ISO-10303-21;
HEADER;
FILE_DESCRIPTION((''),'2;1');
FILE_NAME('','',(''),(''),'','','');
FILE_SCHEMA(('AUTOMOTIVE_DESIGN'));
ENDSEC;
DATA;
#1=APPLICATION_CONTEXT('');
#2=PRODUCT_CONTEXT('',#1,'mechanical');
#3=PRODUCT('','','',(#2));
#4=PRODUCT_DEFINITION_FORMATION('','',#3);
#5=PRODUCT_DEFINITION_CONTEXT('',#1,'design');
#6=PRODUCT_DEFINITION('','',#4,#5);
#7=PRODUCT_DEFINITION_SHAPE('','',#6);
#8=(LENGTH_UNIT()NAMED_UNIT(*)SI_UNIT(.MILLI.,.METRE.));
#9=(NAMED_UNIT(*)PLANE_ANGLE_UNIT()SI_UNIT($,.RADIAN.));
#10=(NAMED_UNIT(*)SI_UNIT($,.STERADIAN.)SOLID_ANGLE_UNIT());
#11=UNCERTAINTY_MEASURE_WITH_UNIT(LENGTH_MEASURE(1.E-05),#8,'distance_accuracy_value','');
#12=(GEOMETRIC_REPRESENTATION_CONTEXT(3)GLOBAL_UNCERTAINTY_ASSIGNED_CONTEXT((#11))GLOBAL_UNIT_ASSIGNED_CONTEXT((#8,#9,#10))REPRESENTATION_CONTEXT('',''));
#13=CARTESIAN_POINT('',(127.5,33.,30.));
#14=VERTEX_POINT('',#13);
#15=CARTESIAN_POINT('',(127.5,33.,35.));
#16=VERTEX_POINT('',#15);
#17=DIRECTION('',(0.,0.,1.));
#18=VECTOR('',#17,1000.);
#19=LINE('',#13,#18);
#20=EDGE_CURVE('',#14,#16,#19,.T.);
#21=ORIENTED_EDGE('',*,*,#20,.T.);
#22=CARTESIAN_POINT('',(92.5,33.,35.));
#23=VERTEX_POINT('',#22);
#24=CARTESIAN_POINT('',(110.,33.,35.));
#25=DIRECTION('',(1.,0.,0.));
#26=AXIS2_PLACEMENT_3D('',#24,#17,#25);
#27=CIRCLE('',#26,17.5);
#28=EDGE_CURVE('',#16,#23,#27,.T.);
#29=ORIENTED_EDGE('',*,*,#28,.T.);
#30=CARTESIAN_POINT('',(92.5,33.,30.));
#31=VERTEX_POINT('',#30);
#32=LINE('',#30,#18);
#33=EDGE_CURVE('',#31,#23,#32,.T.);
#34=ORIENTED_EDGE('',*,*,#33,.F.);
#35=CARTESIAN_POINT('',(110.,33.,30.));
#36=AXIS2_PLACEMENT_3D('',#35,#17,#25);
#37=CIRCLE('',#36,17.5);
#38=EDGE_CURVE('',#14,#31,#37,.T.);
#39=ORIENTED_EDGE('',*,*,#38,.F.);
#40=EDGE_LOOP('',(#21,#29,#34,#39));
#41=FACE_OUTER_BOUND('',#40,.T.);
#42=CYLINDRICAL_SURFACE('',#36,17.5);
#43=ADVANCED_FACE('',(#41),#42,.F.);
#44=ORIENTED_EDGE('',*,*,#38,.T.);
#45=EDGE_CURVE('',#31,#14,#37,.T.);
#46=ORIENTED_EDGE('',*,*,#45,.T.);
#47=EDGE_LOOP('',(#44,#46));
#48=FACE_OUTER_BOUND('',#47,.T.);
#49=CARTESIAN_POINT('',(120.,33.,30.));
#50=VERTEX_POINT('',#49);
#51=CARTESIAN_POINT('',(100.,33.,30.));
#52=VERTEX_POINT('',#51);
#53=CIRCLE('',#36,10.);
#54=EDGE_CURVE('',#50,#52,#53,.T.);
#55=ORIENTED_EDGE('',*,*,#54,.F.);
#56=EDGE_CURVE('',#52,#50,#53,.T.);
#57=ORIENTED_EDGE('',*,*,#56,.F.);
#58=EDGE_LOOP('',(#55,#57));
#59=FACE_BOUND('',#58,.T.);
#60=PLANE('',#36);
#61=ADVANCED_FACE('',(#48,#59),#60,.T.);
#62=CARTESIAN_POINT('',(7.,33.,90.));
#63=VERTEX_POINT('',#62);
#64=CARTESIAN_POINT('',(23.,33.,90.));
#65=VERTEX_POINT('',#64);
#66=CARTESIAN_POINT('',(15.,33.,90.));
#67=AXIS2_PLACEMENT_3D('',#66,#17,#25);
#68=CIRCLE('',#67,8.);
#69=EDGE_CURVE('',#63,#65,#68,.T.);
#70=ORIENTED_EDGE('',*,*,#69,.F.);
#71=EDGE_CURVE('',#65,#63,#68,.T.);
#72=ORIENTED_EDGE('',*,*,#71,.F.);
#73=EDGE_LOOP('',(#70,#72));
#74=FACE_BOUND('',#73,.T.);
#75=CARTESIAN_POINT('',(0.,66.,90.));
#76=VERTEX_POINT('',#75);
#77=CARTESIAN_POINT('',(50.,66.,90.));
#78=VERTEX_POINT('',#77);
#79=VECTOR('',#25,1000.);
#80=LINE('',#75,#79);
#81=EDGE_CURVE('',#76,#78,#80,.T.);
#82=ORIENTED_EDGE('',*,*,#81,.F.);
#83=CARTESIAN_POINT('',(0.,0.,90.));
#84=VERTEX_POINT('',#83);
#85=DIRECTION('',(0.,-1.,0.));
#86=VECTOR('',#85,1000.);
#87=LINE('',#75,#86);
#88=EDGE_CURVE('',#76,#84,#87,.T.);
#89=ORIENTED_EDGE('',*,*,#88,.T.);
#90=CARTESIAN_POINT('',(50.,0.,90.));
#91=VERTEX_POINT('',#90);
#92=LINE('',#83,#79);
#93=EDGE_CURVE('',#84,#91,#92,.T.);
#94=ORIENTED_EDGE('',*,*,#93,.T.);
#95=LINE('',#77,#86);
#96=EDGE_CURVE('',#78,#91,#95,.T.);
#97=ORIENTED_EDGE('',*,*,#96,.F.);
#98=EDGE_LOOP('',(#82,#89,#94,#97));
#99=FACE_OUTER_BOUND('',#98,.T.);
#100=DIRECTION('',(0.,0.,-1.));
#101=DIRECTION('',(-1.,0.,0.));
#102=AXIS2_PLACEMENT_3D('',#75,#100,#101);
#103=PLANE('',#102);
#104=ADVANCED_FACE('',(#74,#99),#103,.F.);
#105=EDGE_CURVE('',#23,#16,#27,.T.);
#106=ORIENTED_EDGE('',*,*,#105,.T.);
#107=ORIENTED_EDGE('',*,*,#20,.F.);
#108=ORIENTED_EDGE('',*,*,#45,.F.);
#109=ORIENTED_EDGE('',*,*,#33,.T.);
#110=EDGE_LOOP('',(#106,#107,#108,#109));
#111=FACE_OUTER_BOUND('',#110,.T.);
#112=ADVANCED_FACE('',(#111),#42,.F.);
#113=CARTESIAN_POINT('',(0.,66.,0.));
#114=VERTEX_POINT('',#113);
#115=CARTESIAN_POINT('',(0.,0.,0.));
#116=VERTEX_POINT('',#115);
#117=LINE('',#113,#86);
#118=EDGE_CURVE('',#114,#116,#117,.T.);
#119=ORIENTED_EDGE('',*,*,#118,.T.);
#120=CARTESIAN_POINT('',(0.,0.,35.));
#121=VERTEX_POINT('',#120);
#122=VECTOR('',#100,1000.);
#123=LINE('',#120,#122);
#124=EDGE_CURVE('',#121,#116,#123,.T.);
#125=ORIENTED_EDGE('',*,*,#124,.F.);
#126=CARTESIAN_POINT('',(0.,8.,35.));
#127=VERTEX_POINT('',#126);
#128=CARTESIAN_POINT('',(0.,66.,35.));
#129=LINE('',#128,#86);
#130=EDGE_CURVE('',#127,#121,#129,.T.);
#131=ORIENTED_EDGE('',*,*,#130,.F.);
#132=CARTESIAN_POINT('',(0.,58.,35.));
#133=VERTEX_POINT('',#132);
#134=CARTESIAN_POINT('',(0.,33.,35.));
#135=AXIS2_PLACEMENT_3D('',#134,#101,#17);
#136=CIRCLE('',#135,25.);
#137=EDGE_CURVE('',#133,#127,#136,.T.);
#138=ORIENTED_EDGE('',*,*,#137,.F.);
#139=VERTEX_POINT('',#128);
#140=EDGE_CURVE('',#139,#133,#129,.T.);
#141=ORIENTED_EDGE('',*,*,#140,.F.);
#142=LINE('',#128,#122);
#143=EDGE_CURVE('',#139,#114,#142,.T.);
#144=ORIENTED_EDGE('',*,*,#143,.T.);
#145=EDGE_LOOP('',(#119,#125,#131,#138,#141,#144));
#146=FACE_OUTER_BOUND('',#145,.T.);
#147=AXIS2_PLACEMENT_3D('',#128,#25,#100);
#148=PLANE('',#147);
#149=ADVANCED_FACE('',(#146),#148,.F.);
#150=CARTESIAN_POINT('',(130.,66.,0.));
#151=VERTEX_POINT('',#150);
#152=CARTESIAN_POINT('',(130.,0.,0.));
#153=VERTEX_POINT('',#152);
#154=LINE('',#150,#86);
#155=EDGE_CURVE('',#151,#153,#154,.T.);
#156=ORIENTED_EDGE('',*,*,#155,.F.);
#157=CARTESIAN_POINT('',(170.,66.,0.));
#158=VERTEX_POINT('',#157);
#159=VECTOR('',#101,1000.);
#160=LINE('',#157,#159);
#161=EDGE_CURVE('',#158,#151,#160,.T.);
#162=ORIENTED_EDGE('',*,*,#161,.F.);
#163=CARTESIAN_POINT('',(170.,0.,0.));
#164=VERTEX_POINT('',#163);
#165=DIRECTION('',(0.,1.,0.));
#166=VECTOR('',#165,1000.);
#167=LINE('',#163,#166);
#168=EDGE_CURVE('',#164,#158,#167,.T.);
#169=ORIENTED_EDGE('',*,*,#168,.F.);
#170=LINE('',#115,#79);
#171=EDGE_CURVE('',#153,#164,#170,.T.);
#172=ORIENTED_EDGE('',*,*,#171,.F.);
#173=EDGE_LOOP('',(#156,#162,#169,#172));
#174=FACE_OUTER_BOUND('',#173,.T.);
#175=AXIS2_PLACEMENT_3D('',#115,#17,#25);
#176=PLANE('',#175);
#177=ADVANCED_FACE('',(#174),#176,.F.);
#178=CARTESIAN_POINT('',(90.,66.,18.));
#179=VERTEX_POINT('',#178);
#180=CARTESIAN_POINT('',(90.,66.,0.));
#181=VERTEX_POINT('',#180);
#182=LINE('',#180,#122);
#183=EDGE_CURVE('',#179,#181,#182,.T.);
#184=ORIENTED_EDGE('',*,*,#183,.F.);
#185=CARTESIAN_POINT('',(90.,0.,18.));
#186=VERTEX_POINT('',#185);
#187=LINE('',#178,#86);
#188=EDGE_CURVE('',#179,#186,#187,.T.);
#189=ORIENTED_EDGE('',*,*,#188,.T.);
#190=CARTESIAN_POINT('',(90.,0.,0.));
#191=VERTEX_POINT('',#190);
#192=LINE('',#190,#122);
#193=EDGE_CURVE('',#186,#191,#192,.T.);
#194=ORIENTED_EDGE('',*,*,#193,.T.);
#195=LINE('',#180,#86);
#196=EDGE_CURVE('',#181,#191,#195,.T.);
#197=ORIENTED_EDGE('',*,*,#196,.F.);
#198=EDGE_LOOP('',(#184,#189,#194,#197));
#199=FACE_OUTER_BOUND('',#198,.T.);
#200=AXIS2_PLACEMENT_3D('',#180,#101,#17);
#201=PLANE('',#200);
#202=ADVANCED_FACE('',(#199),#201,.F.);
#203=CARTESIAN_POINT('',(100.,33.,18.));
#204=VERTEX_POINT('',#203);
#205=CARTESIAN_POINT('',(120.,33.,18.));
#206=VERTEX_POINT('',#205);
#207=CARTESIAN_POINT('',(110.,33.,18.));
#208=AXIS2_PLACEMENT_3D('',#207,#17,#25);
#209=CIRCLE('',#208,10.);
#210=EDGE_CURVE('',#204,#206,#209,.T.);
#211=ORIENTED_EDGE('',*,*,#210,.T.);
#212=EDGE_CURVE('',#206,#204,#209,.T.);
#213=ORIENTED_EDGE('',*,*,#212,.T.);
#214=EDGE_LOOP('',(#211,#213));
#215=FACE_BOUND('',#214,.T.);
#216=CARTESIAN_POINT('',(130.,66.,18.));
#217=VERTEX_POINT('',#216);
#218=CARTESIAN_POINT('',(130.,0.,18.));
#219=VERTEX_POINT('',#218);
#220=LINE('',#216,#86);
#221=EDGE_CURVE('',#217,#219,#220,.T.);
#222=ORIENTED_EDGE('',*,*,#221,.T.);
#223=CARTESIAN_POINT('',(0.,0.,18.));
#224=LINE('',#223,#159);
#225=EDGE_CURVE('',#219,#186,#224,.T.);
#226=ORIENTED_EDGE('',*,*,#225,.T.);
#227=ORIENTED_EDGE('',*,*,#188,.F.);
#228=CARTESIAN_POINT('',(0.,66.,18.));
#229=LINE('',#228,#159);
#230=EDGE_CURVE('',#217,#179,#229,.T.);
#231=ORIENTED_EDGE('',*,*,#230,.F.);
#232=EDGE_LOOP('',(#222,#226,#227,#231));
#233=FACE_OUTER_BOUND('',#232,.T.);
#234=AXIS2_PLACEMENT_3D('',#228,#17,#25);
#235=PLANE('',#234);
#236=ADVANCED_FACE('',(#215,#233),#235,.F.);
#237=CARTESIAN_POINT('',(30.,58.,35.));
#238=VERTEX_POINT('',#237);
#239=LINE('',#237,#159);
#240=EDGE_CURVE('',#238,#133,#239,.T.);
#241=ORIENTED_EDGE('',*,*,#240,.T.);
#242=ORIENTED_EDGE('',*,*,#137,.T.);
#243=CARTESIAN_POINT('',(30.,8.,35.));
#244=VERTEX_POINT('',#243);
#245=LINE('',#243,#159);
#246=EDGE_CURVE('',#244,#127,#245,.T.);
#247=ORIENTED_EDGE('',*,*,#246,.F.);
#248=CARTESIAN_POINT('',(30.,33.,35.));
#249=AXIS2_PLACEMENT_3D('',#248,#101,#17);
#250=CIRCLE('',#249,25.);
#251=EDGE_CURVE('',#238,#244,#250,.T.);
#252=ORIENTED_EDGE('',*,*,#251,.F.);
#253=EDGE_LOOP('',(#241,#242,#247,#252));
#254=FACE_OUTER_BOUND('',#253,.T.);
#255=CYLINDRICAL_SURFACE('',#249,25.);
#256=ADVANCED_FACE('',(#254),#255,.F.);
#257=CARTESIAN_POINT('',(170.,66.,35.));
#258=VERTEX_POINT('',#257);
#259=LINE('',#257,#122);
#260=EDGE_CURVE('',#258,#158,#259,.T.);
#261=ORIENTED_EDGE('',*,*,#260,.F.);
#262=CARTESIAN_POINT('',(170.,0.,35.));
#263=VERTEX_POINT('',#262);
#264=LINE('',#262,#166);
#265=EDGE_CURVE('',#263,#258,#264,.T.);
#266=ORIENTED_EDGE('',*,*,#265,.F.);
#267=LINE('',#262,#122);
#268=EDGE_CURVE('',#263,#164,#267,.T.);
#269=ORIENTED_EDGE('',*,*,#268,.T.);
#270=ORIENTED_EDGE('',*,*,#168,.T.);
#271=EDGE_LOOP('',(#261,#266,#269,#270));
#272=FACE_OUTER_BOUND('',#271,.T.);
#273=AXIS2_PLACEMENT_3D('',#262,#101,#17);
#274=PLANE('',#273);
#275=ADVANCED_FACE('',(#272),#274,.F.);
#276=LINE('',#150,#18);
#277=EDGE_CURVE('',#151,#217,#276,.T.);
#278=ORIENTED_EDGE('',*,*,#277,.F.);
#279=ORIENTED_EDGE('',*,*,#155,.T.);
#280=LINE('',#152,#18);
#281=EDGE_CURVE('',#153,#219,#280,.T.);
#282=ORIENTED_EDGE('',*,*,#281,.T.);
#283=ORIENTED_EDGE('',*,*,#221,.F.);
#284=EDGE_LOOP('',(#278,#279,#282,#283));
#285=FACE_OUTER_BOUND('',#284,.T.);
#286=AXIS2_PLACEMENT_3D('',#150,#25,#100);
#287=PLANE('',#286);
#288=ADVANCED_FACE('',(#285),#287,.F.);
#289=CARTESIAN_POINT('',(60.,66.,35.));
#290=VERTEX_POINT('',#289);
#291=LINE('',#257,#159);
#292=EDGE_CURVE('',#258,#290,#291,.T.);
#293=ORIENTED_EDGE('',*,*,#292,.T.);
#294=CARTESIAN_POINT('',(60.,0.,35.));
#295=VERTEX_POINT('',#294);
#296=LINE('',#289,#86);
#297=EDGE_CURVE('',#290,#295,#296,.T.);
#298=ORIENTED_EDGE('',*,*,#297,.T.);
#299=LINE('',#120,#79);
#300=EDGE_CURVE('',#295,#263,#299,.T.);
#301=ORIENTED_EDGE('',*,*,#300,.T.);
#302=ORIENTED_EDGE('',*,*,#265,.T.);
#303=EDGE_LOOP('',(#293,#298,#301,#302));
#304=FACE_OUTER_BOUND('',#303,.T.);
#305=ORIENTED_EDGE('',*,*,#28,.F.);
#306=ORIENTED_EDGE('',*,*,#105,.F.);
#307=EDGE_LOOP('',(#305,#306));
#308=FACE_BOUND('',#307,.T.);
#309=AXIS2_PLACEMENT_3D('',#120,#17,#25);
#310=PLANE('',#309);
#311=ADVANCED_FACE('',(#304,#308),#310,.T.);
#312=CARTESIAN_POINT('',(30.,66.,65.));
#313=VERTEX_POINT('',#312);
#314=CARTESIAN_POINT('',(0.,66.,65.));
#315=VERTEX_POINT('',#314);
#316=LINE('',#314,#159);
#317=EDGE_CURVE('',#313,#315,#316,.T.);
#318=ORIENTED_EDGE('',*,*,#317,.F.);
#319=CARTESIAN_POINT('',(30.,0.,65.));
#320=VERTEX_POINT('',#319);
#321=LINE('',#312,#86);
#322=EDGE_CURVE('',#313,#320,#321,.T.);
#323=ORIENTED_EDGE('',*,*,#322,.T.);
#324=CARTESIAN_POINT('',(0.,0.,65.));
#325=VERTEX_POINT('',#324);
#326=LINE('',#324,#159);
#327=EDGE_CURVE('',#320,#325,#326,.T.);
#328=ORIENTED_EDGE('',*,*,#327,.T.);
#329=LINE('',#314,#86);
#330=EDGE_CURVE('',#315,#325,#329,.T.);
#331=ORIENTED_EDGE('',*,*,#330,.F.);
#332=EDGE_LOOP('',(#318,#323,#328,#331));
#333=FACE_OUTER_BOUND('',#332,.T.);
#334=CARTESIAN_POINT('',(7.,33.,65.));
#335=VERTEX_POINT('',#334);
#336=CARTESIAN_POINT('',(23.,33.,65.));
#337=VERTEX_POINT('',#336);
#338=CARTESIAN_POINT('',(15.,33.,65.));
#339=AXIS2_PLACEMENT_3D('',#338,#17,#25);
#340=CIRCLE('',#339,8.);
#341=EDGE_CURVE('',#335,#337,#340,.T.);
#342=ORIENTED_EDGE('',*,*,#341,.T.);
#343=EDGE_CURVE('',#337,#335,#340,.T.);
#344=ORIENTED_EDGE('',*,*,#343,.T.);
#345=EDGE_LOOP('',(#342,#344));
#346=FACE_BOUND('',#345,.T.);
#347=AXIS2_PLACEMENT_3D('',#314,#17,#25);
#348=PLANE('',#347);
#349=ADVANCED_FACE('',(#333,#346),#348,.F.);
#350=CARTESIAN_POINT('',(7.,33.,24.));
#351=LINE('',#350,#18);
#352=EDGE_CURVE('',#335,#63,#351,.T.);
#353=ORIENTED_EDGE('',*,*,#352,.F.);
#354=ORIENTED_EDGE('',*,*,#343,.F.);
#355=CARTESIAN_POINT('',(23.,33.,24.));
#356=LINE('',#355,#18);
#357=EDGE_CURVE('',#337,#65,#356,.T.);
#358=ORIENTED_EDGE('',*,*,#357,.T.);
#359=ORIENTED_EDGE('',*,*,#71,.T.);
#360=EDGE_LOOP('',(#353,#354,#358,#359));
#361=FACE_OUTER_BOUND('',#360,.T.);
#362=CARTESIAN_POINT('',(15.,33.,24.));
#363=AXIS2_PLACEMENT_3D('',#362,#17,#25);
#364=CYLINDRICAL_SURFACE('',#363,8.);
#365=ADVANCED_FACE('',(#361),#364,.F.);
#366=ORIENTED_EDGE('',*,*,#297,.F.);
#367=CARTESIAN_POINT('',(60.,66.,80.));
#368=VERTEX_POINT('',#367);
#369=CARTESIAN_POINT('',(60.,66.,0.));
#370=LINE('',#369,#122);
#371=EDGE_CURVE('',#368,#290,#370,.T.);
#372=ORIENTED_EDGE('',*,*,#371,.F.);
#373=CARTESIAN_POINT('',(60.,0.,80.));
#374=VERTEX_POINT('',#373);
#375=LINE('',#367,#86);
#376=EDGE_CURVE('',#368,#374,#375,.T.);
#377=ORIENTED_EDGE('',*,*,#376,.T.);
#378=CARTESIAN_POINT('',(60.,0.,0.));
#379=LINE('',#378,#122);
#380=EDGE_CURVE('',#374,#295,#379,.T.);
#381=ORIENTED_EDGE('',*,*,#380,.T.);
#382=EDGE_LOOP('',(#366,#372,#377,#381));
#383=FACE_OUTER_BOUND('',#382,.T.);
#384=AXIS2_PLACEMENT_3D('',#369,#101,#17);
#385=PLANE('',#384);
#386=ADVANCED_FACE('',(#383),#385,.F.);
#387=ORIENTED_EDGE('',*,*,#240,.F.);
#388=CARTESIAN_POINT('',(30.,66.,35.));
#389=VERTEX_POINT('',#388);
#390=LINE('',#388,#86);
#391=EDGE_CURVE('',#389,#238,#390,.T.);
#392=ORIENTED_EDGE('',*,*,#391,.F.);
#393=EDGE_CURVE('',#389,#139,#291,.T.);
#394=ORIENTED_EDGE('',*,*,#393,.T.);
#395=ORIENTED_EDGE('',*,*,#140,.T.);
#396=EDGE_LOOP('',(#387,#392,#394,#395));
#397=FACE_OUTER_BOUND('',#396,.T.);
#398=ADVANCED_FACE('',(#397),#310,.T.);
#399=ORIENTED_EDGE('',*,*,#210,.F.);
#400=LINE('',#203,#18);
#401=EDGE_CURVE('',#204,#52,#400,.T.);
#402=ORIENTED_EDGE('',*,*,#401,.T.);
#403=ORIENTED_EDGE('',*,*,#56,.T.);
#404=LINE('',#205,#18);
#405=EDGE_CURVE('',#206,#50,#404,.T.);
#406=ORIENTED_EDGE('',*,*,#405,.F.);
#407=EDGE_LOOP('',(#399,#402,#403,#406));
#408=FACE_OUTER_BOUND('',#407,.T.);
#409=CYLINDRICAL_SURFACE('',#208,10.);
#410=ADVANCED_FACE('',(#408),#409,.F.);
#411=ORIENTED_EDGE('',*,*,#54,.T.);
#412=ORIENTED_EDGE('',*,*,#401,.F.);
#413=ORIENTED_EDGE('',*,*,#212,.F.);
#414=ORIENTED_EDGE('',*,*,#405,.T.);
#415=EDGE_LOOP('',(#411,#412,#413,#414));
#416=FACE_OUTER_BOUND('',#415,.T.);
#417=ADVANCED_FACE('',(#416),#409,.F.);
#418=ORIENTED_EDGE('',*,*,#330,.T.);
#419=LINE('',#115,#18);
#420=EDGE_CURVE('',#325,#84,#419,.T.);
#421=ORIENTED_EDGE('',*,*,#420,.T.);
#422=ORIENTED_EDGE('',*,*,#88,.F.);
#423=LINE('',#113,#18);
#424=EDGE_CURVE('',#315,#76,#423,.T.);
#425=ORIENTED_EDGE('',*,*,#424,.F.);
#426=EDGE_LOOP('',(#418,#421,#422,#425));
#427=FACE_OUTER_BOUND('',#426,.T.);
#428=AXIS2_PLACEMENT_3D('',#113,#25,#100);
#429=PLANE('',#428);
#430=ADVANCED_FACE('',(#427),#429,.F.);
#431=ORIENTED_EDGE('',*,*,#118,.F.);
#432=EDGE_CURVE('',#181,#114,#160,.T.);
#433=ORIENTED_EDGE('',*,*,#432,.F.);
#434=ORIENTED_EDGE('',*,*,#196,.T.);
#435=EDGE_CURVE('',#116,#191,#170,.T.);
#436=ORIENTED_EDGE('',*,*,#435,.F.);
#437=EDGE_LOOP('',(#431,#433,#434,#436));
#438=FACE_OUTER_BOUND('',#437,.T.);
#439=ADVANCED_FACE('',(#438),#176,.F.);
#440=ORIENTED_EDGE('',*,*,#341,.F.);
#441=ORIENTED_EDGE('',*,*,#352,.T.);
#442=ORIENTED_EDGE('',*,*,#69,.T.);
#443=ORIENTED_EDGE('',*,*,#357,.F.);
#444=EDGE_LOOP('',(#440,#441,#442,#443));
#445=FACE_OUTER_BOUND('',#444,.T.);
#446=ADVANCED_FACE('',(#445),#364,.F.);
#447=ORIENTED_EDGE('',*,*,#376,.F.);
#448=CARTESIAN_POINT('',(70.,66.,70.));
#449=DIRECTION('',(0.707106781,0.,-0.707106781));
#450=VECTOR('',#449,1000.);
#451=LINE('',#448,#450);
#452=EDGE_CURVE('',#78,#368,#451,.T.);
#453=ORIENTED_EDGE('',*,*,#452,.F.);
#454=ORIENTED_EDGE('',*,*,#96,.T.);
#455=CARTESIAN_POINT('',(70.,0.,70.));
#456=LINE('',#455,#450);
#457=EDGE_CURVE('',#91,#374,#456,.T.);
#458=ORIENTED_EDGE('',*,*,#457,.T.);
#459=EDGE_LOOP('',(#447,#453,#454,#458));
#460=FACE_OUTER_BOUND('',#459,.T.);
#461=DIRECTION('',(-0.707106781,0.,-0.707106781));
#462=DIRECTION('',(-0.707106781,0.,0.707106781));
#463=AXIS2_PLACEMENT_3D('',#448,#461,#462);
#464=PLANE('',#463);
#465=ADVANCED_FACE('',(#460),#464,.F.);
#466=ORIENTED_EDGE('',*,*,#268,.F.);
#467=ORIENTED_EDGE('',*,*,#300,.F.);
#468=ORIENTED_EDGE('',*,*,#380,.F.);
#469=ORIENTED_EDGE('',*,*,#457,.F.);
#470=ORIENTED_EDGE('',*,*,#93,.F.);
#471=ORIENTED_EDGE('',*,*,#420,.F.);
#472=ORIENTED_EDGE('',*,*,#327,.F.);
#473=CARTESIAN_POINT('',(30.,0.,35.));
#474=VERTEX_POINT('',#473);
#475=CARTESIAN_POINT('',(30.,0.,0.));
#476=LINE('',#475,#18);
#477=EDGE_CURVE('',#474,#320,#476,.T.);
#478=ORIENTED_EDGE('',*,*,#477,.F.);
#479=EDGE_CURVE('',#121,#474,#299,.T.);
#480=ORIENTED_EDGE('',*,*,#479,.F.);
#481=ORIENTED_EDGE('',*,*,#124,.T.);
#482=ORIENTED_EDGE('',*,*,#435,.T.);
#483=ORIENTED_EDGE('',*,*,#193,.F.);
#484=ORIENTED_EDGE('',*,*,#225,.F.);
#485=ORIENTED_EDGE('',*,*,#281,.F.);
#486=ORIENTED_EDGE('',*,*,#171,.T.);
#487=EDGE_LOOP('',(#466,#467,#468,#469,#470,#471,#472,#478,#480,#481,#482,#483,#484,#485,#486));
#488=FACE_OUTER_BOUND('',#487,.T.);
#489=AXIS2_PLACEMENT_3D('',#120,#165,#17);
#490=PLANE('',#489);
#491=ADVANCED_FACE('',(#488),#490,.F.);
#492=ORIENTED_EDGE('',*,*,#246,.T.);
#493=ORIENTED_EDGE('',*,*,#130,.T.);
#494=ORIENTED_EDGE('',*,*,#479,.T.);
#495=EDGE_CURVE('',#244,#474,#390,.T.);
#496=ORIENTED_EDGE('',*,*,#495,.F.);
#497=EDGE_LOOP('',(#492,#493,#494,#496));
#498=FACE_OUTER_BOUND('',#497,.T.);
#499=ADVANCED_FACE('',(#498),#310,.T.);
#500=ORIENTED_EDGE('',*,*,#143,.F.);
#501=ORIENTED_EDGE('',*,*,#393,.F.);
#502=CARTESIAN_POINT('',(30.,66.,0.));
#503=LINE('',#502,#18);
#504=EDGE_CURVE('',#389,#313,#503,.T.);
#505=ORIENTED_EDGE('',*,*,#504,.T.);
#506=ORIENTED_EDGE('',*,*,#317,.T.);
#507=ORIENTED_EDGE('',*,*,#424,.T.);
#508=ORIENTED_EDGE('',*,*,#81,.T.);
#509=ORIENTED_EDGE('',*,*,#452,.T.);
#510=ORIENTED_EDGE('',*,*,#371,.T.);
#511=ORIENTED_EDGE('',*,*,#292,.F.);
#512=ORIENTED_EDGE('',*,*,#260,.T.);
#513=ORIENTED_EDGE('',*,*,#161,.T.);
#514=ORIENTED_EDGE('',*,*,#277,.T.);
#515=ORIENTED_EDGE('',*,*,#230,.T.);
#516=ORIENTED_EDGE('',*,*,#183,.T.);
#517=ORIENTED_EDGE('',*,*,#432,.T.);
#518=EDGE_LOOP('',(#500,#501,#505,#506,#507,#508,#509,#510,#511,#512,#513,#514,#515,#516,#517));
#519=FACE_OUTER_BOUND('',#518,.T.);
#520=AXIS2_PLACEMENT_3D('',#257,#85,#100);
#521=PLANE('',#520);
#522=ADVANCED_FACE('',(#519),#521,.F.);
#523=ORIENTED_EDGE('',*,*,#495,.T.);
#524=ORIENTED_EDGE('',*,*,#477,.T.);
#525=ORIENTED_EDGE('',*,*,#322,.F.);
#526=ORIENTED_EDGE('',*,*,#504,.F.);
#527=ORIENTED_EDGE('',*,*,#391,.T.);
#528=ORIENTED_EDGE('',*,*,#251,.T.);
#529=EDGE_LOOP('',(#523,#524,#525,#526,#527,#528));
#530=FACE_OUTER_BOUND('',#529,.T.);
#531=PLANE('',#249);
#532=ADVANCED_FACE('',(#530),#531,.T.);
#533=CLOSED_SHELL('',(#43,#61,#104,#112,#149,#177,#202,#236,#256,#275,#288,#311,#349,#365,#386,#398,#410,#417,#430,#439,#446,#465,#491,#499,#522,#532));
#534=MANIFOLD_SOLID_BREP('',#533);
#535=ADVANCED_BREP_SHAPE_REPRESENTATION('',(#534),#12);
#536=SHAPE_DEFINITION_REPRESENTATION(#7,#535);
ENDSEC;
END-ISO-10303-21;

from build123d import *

# Parameters (mm, degrees)
BASE_BLOCK_PROFILE_W    = 170
BASE_BLOCK_PROFILE_H    = 66
BASE_BLOCK_DEPTH        = 35
SLOT_CUT_DEPTH          = 66
COUNTERBORE_35_SKETCH_R = 17.5
COUNTERBORE_35_DEPTH    = 5
HOLE_20_SKETCH_R        = 10
HOLE_20_DEPTH           = 12
ROUNDED_CUT_DEPTH       = 30
SIDE_LUG_DEPTH          = 66
LUG_HOLE_16_SKETCH_R    = 8
LUG_HOLE_16_DEPTH       = 66


with BuildPart() as part:
    # Base Block Profile → Base Block (new body)
    with BuildSketch(Plane.XY):
        with Locations((85, 33)):
            Rectangle(BASE_BLOCK_PROFILE_W, BASE_BLOCK_PROFILE_H)
    extrude(amount=BASE_BLOCK_DEPTH)

    # Slot Profile → Slot Cut (cut)
    with BuildSketch(Plane.XZ):
        Polygon((110, 0), (130, 0), (130, 18), (90, 18), (90, 0), align=None)
    extrude(amount=-SLOT_CUT_DEPTH, mode=Mode.SUBTRACT)

    # Counterbore Ø35 Sketch → Counterbore Ø35 (cut)
    with BuildSketch(Plane.XY.offset(35)):
        with Locations((110, 33)):
            Circle(COUNTERBORE_35_SKETCH_R)
    extrude(amount=-COUNTERBORE_35_DEPTH, mode=Mode.SUBTRACT)

    # Hole Ø20 Sketch → Hole Ø20 (cut)
    with BuildSketch(Plane.XY.offset(30)):
        with Locations((110, 33)):
            Circle(HOLE_20_SKETCH_R)
    extrude(amount=-HOLE_20_DEPTH, mode=Mode.SUBTRACT)

    # Rounded Cut Sketch → Rounded Cut (cut)
    with BuildSketch(Plane.ZY):
        with BuildLine():
            Line((35, 58), (35, 8))
            ThreePointArc((35, 8), (10, 33), (35, 58))
        make_face()
    extrude(amount=-ROUNDED_CUT_DEPTH, mode=Mode.SUBTRACT)

    # Side Lug Profile → Side Lug (add)
    with BuildSketch(Plane.XZ):
        Polygon((30, 65), (30, 35), (60, 35), (60, 80), (50, 90), (0, 90), (0, 65), align=None)
    extrude(amount=-SIDE_LUG_DEPTH)

    # Lug Hole Ø16 Sketch → Lug Hole Ø16 (cut)
    with BuildSketch(Plane.XY.offset(90)):
        with Locations((15, 33)):
            Circle(LUG_HOLE_16_SKETCH_R)
    extrude(amount=-LUG_HOLE_16_DEPTH, mode=Mode.SUBTRACT)


solid = part.part
